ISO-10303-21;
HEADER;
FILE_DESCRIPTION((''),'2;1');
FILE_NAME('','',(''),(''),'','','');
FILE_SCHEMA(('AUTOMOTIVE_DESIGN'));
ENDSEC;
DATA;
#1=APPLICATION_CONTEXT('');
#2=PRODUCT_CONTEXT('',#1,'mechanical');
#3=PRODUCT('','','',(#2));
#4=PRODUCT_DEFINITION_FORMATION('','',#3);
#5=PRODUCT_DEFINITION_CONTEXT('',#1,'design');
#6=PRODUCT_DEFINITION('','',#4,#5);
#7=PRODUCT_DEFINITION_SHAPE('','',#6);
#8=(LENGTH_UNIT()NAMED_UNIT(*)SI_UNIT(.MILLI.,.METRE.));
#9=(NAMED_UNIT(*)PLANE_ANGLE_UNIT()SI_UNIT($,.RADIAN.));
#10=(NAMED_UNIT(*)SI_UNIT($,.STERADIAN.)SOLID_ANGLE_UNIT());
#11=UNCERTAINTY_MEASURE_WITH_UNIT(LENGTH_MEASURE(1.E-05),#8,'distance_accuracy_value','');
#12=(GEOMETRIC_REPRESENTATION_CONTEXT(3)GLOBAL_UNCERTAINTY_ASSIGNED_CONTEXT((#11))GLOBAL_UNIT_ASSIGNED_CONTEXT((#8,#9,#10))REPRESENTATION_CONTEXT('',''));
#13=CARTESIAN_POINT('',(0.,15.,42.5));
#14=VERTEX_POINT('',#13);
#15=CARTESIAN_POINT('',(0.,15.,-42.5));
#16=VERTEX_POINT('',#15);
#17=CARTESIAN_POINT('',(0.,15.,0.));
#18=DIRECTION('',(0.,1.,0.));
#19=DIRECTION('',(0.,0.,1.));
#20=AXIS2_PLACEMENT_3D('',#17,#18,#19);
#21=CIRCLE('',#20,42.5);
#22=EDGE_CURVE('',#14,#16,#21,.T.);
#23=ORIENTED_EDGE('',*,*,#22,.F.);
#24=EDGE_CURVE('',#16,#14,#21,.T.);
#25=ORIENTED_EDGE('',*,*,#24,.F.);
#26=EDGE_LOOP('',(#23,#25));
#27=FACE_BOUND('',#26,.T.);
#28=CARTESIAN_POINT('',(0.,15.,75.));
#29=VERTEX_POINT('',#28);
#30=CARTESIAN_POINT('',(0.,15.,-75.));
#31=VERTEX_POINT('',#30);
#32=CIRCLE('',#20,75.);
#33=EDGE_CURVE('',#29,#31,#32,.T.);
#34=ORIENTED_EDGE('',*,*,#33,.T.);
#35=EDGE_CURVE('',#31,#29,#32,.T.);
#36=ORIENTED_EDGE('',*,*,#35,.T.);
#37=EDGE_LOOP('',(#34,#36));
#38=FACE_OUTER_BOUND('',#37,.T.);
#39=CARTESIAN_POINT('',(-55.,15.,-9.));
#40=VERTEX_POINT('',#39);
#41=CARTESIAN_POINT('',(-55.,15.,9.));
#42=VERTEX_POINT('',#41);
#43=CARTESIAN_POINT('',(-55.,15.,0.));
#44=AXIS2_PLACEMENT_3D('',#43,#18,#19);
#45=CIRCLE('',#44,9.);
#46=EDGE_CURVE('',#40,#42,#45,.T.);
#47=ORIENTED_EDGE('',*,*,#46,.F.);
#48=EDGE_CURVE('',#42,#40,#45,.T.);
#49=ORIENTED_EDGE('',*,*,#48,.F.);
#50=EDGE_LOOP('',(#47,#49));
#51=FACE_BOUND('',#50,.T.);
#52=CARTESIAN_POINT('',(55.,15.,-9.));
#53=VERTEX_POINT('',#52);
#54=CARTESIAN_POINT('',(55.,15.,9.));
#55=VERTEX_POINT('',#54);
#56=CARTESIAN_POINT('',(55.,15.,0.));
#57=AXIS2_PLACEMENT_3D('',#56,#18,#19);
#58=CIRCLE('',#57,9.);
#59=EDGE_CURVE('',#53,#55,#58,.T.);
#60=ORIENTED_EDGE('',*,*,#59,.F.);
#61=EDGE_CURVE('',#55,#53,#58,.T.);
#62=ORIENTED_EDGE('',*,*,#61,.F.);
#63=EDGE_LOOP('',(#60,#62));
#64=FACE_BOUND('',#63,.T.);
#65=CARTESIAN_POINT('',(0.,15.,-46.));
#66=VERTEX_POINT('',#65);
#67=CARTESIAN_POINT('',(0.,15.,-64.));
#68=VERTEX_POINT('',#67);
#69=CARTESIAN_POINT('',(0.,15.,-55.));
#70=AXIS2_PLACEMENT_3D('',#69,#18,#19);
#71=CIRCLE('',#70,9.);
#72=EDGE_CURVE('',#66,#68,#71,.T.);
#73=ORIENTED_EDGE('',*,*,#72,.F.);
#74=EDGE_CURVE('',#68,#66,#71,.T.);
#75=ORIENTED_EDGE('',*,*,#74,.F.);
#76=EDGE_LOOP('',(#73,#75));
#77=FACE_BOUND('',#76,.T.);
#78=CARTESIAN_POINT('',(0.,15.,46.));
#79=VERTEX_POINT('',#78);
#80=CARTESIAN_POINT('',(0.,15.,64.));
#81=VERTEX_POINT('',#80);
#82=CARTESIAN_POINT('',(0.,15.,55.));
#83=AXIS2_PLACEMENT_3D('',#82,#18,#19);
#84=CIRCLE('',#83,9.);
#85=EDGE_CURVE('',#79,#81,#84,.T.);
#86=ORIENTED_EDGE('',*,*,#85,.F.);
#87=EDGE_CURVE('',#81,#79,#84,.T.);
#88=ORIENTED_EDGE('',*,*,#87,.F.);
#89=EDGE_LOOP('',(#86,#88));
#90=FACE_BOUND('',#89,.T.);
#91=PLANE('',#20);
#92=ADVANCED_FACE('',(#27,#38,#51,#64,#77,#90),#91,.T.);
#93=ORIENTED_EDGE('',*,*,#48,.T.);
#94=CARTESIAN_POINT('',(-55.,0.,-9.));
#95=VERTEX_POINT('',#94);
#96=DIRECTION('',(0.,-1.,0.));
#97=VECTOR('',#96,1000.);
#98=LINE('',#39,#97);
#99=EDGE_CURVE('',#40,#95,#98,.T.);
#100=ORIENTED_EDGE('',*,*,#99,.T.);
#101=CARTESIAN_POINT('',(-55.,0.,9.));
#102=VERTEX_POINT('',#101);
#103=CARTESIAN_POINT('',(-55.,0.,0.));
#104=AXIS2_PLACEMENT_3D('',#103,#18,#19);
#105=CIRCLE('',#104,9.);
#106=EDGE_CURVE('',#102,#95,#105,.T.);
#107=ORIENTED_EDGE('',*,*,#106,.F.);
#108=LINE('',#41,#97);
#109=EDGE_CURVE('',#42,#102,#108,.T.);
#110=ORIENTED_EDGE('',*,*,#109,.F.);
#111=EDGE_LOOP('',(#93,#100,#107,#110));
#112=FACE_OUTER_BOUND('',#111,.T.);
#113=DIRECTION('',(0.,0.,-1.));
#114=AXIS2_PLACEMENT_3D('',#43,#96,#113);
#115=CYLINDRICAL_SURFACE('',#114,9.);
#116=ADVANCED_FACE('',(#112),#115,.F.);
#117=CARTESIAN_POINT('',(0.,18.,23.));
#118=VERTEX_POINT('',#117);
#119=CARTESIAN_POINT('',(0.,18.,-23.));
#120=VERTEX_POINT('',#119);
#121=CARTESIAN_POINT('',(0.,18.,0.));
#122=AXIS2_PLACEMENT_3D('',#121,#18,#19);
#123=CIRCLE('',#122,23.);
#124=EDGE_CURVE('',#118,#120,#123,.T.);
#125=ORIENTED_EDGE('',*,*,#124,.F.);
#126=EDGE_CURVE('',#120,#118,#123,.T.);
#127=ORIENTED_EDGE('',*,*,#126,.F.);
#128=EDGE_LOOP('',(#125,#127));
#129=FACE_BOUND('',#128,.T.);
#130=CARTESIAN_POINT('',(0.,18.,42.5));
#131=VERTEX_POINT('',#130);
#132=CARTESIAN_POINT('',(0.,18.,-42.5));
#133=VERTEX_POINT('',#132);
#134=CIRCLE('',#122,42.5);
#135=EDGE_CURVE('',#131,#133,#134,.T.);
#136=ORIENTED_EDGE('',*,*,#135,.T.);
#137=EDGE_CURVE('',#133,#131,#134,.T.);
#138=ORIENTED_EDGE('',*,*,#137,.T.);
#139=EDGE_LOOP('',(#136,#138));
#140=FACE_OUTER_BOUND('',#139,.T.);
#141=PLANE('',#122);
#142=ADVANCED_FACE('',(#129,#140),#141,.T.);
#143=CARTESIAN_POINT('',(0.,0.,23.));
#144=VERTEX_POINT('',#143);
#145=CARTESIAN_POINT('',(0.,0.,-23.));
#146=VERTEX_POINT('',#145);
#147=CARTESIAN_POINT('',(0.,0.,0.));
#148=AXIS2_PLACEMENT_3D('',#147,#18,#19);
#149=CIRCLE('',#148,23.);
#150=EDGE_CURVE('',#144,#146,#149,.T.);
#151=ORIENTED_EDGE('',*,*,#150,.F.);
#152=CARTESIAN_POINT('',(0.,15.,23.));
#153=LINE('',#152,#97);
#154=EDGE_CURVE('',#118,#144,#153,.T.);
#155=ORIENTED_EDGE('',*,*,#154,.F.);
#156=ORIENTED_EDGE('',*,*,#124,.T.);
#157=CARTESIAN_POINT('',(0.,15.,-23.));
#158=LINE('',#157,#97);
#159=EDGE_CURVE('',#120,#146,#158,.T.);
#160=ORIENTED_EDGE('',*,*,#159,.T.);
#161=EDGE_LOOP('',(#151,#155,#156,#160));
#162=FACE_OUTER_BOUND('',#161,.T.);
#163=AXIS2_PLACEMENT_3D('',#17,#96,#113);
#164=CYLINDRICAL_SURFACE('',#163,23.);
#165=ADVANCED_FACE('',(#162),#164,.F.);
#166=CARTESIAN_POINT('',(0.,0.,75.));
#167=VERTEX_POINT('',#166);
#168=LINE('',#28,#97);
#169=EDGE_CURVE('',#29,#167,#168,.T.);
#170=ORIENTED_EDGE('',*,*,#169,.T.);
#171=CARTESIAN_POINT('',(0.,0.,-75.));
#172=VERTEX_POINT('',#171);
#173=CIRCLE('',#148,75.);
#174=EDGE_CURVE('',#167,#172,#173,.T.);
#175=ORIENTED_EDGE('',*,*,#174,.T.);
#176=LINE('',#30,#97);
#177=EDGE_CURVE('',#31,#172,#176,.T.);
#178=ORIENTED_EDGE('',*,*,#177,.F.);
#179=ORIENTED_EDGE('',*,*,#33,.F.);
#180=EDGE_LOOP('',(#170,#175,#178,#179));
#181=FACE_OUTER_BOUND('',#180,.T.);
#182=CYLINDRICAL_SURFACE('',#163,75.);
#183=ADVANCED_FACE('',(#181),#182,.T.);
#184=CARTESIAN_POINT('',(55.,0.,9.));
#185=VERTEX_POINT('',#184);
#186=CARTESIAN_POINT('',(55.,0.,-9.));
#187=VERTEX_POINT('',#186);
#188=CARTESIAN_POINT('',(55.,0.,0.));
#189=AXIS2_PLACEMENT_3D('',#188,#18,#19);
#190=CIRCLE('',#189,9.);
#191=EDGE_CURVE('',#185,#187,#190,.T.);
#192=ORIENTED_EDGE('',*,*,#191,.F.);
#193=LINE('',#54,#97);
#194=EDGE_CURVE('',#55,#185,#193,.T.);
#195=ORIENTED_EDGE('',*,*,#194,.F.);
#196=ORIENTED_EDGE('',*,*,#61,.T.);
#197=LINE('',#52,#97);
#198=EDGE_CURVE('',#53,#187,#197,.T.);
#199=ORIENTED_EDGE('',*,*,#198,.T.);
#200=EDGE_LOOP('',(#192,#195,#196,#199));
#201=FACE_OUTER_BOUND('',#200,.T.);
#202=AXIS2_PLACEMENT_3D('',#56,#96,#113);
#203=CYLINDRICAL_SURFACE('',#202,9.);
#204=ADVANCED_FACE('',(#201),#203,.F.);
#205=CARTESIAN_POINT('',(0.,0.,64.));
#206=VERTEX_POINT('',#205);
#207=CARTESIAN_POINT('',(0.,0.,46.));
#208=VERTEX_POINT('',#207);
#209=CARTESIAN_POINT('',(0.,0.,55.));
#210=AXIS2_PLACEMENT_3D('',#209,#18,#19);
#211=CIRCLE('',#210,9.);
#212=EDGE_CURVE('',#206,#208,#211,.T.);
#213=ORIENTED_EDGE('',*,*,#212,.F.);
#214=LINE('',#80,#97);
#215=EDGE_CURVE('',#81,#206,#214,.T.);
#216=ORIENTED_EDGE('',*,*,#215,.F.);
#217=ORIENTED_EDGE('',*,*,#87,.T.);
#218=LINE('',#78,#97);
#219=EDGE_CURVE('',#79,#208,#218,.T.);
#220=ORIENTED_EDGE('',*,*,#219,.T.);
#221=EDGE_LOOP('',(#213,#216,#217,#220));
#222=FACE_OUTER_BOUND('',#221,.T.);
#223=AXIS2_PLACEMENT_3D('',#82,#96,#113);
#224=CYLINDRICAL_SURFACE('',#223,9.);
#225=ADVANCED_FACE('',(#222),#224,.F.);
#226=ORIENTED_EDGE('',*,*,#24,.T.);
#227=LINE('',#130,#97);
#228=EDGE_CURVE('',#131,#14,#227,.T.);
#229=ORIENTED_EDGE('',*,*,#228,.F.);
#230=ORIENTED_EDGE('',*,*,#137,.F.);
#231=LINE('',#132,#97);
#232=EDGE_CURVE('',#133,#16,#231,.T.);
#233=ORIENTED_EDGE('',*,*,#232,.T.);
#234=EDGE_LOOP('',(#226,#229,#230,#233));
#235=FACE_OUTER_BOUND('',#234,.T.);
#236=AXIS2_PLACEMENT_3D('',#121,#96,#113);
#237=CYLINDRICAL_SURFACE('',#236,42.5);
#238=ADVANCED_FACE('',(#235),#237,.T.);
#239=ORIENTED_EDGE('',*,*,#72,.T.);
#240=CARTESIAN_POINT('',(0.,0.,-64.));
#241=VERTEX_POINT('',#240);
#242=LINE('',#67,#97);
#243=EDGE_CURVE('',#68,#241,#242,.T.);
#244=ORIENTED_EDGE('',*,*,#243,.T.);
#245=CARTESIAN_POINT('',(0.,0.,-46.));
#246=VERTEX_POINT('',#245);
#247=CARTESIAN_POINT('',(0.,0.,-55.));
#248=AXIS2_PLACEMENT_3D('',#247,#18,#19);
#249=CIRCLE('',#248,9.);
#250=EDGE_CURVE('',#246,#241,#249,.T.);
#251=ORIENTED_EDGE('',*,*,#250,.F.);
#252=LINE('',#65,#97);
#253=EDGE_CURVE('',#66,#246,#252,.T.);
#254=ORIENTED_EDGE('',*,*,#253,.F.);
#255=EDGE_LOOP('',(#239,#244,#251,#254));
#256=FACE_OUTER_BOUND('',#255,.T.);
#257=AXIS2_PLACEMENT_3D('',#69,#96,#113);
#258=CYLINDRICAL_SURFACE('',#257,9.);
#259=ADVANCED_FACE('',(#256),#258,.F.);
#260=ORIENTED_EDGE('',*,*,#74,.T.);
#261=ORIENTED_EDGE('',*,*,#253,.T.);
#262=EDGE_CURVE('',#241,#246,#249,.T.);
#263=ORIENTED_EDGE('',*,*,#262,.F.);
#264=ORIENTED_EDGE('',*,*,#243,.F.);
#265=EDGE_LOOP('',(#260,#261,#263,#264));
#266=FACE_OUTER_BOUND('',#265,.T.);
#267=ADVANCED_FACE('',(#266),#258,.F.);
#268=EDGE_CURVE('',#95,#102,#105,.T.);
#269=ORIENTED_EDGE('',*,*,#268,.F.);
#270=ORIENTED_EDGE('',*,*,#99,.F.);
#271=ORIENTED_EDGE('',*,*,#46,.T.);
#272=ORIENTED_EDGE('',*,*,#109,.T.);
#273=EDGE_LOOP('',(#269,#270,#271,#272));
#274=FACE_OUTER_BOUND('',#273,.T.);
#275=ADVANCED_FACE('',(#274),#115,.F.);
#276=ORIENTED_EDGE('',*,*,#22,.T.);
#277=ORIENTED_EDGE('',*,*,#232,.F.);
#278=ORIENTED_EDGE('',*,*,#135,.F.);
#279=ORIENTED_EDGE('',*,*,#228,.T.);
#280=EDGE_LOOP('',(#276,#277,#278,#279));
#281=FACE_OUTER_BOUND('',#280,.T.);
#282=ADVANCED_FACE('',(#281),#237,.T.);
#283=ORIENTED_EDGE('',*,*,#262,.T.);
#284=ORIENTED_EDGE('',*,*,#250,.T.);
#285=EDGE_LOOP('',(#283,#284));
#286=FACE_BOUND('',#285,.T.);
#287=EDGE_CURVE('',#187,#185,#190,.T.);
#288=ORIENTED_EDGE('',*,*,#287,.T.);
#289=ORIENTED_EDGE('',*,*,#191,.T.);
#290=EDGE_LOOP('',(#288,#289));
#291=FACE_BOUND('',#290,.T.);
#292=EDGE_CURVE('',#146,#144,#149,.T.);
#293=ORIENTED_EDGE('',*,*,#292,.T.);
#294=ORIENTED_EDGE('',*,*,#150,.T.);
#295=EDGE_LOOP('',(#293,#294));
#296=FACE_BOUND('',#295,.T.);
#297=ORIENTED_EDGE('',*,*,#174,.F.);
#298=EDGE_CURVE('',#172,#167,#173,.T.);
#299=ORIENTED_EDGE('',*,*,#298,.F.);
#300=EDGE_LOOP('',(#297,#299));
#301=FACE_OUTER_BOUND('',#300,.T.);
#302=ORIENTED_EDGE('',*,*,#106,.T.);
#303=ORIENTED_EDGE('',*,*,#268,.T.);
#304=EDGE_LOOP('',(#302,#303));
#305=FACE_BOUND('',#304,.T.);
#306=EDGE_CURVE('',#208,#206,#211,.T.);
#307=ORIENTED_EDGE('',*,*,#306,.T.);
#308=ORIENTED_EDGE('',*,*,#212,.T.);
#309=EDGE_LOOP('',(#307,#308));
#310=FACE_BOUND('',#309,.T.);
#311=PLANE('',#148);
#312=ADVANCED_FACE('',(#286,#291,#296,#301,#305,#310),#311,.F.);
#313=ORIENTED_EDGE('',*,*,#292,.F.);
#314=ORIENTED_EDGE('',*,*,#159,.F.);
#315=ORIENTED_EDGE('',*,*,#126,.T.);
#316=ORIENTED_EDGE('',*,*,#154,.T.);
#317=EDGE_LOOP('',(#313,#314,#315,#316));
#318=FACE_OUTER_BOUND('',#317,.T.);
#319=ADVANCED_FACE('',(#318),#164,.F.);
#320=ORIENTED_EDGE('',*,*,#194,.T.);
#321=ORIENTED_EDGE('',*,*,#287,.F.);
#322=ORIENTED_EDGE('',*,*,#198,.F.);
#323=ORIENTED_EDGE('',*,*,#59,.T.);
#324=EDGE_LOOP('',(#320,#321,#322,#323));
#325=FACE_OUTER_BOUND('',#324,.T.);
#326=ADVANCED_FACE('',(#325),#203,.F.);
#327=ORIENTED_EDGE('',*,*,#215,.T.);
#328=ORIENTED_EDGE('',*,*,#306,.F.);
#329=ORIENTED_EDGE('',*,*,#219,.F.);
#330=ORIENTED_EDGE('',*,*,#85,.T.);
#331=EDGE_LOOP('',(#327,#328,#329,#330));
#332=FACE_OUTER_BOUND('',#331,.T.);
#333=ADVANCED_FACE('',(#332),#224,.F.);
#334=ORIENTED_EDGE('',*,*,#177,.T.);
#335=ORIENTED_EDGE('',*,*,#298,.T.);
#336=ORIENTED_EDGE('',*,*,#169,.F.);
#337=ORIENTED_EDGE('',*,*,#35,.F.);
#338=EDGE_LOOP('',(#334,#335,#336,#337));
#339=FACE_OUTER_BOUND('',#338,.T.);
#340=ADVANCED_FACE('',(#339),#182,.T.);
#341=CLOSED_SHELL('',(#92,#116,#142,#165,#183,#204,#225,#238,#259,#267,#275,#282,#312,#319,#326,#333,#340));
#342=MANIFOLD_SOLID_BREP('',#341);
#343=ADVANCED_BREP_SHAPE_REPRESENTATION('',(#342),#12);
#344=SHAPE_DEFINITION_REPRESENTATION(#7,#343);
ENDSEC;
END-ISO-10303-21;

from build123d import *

# Parameters (mm, degrees)
SKETCH_1_R      = 75
SKETCH_1_R_2    = 9
SKETCH_1_R_3    = 23
EXTRUDE_1_DEPTH = 15
SKETCH_2_R      = 42.5
SKETCH_2_R_2    = 23
EXTRUDE_2_DEPTH = 3


with BuildPart() as part:
    # 草图1 → 凸台-拉伸1 (new body)
    with BuildSketch(Plane(origin=(0, 0, 0), x_dir=(1, 0, 0), z_dir=(0, 1, 0))):
        with Locations(Location((0, 0, 0), (0, 0, 270))):
            Circle(SKETCH_1_R)
        with Locations(Location((0, 55, 0), (0, 0, 270))):
            Circle(SKETCH_1_R_2, mode=Mode.SUBTRACT)
        with Locations(Location((55, 0, 0), (0, 0, 270))):
            Circle(SKETCH_1_R_2, mode=Mode.SUBTRACT)
        with Locations(Location((0, -55, 0), (0, 0, 270))):
            Circle(SKETCH_1_R_2, mode=Mode.SUBTRACT)
        with Locations(Location((-55, 0, 0), (0, 0, 270))):
            Circle(SKETCH_1_R_2, mode=Mode.SUBTRACT)
        with Locations(Location((0, 0, 0), (0, 0, 270))):
            Circle(SKETCH_1_R_3, mode=Mode.SUBTRACT)
    extrude(amount=EXTRUDE_1_DEPTH)

    # 草图2 → 凸台-拉伸2 (add)
    with BuildSketch(Plane(origin=(0, 15, 0), x_dir=(1, 0, 0), z_dir=(0, 1, 0))):
        with Locations(Location((0, 0, 0), (0, 0, 270))):
            Circle(SKETCH_2_R)
        with Locations(Location((0, 0, 0), (0, 0, 270))):
            Circle(SKETCH_2_R_2, mode=Mode.SUBTRACT)
    extrude(amount=EXTRUDE_2_DEPTH)


solid = part.part
